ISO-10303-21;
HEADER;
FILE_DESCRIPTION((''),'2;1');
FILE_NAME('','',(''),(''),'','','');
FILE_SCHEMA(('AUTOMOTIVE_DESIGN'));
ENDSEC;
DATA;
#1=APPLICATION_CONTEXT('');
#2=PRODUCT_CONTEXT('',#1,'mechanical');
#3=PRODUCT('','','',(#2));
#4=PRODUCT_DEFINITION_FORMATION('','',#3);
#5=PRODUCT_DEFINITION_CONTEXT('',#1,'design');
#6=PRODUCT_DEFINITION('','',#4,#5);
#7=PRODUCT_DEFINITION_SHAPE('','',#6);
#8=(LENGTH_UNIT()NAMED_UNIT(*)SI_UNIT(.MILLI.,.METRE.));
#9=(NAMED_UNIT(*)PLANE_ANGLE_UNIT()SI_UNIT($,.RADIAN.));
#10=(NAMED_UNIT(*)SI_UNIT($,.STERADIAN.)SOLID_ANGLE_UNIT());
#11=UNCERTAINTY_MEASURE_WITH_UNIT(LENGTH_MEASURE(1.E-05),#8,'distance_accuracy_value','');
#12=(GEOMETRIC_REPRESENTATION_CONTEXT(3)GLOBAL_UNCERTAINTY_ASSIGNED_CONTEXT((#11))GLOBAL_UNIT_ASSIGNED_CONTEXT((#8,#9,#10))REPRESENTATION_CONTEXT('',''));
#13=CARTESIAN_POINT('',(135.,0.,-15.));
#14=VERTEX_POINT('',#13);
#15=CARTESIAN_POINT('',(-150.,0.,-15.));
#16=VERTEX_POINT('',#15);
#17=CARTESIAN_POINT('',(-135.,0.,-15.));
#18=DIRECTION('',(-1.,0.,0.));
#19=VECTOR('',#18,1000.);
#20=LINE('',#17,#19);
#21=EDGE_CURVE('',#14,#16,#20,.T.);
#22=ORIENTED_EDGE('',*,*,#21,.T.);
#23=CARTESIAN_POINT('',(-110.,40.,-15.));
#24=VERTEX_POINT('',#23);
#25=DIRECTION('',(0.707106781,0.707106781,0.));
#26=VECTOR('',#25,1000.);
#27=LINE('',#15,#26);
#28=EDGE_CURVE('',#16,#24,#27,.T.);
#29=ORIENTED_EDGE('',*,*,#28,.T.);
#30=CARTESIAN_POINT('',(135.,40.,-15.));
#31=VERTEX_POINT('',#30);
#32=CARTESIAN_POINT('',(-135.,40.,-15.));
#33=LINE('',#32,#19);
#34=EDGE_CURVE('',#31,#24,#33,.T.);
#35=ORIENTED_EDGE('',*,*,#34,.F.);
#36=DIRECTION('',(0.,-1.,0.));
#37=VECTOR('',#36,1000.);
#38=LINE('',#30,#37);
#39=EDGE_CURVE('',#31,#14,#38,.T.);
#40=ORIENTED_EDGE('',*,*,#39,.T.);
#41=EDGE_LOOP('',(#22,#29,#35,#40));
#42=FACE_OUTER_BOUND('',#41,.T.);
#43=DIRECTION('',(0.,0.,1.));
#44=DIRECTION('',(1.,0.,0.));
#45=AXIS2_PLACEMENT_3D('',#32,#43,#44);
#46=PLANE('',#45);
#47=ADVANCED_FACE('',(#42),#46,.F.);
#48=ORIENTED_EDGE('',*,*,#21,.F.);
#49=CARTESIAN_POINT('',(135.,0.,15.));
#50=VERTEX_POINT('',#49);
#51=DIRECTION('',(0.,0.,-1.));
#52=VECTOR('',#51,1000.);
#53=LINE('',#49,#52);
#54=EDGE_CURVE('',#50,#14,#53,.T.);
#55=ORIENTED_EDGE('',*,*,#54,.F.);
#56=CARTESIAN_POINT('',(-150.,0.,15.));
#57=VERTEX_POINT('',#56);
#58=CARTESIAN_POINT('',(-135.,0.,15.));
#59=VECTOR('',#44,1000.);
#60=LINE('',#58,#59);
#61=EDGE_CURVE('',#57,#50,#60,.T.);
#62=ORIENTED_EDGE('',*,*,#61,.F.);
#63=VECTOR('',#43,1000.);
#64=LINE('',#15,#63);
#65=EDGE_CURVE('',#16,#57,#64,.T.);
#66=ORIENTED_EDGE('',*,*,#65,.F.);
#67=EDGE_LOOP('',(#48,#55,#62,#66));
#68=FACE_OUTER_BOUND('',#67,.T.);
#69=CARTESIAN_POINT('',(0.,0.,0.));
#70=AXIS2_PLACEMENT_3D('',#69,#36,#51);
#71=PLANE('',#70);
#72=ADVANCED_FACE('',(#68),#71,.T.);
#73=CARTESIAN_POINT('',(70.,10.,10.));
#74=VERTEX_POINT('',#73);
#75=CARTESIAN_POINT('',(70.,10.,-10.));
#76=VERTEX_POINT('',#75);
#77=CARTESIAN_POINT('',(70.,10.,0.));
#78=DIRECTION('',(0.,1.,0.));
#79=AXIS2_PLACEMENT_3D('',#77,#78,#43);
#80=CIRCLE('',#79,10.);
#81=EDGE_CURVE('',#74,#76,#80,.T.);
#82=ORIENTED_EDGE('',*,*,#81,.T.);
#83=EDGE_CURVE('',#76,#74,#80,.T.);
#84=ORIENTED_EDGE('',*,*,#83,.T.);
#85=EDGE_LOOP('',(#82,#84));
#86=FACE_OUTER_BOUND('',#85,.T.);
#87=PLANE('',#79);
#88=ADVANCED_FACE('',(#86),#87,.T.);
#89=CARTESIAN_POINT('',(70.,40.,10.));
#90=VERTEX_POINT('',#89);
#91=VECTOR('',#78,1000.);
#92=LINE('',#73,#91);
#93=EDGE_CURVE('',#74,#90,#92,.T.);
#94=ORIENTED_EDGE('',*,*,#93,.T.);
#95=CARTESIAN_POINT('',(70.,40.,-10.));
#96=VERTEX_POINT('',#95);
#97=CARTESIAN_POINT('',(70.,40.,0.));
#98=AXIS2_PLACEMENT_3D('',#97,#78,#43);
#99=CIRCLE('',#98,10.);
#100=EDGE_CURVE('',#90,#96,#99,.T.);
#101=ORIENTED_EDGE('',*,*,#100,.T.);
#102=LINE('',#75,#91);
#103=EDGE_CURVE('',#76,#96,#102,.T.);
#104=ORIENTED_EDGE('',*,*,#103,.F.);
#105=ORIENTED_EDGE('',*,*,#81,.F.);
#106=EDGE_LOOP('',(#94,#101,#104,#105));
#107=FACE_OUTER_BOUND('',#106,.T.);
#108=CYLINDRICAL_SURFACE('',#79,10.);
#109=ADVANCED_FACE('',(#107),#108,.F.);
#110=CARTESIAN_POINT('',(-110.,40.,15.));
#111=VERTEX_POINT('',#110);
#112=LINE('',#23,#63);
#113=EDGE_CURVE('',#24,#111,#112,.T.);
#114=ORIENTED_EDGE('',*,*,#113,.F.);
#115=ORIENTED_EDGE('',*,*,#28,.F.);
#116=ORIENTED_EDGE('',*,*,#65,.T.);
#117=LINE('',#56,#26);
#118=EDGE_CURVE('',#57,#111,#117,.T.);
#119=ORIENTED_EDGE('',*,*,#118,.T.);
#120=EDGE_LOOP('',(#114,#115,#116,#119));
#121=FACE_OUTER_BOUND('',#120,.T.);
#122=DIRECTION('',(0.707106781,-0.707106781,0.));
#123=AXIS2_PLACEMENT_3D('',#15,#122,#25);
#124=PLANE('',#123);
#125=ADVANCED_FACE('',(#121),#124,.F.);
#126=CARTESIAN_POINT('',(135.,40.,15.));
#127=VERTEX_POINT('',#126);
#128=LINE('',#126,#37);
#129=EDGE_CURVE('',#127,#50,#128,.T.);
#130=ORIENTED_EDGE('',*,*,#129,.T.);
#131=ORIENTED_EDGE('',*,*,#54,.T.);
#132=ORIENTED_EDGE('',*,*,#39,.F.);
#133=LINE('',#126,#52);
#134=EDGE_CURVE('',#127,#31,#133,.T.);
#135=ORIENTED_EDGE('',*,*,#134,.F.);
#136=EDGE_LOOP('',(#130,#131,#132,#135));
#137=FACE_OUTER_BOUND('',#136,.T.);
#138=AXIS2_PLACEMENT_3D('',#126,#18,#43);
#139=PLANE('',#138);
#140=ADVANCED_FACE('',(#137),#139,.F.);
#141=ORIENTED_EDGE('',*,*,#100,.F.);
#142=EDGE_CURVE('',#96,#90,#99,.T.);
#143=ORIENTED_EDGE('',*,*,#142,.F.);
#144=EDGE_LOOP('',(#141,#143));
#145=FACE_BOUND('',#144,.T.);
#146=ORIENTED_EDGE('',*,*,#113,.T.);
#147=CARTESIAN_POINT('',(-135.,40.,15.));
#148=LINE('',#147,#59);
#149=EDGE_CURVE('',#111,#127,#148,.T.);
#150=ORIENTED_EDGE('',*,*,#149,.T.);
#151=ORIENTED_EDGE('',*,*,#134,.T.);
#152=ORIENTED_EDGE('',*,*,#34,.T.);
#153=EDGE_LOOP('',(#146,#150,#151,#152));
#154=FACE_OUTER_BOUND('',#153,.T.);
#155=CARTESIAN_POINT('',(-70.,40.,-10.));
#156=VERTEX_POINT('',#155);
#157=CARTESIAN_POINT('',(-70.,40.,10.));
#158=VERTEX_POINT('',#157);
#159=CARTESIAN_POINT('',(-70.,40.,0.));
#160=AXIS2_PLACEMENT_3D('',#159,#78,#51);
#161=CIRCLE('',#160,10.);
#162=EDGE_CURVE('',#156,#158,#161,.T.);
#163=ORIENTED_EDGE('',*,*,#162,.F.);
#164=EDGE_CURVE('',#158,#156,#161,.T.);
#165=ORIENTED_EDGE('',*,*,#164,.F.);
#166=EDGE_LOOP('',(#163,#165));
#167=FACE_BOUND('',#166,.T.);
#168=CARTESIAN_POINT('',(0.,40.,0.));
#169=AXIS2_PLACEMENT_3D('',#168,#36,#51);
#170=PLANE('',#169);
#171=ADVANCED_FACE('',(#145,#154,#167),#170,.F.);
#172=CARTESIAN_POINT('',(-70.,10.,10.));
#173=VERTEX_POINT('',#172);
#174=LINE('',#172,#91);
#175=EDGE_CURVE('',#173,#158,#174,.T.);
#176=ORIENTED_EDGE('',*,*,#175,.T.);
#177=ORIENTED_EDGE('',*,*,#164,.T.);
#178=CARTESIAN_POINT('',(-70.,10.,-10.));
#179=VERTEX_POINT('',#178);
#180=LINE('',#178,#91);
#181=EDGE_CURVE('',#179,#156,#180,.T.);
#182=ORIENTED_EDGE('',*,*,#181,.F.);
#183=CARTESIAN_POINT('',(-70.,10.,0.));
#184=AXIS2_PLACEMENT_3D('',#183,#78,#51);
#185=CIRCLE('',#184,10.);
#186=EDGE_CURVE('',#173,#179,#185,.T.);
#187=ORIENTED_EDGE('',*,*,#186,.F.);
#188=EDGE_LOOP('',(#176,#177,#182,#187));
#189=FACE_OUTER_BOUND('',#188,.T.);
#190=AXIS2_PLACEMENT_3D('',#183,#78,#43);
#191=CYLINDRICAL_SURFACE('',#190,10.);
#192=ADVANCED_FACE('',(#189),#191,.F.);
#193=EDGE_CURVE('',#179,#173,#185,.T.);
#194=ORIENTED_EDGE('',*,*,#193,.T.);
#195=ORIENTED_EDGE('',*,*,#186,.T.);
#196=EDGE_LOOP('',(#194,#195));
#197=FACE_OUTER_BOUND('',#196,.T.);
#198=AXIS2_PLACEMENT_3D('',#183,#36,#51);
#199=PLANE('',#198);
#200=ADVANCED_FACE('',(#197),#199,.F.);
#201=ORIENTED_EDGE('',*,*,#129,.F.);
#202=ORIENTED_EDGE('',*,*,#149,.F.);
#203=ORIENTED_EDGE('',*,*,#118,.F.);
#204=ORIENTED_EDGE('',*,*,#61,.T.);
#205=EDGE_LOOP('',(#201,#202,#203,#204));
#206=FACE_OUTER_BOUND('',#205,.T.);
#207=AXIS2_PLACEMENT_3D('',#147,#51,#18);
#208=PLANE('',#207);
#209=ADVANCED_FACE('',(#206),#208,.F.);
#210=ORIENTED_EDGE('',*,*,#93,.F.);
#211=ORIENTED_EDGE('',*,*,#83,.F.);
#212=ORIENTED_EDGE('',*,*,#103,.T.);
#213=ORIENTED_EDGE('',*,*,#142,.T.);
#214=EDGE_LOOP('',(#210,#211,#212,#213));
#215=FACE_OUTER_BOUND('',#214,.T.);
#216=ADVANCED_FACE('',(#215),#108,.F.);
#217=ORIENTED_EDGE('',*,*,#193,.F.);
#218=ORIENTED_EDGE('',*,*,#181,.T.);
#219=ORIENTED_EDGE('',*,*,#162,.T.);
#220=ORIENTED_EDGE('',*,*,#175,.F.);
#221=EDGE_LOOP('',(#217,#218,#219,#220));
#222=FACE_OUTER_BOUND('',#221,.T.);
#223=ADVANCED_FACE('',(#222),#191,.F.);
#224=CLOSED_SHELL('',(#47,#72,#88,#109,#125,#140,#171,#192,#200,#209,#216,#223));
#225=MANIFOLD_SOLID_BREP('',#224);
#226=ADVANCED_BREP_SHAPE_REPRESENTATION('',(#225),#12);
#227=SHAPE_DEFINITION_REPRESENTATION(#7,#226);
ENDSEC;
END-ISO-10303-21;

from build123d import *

# Parameters (mm, degrees)
SKETCH_1_W          = 270
SKETCH_1_H          = 30
EXTRUDE_1_DEPTH     = 40
SKETCH_2_R          = 10
CUT_EXTRUDE_2_DEPTH = 30
SKETCH_3_W          = 30
SKETCH_3_H          = 40
EXTRUDE_2_DEPTH     = 15
CUT_EXTRUDE_3_DEPTH = 159.113883008


with BuildPart() as part:
    # 草图1 → 凸台-拉伸1 (new body)
    with BuildSketch(Plane(origin=(0, 0, 0), x_dir=(1, 0, 0), z_dir=(0, 1, 0))):
        Rectangle(SKETCH_1_W, SKETCH_1_H)
    extrude(amount=EXTRUDE_1_DEPTH)

    # 草图2 → 切除-拉伸2 (cut)
    with BuildSketch(Plane(origin=(0, 40, 0), x_dir=(1, 0, 0), z_dir=(0, 1, 0))):
        with Locations(Location((70, 0, 0), (0, 0, 270))):
            Circle(SKETCH_2_R)
        with Locations(Location((-70, 0, 0), (0, 0, 90))):
            Circle(SKETCH_2_R)
    extrude(amount=-CUT_EXTRUDE_2_DEPTH, mode=Mode.SUBTRACT)

    # 草图3 → 凸台-拉伸2 (add)
    with BuildSketch(Plane.ZY.offset(135)):
        with Locations((0, 20)):
            Rectangle(SKETCH_3_W, SKETCH_3_H)
    extrude(amount=EXTRUDE_2_DEPTH)

    # 草图4 → 切除-拉伸3 (cut, through all)
    with BuildSketch(Plane.XY.offset(15)):
        Polygon((-150, 0), (-110, 40), (-150, 40), align=None)
    extrude(amount=-CUT_EXTRUDE_3_DEPTH, mode=Mode.SUBTRACT)


solid = part.part
